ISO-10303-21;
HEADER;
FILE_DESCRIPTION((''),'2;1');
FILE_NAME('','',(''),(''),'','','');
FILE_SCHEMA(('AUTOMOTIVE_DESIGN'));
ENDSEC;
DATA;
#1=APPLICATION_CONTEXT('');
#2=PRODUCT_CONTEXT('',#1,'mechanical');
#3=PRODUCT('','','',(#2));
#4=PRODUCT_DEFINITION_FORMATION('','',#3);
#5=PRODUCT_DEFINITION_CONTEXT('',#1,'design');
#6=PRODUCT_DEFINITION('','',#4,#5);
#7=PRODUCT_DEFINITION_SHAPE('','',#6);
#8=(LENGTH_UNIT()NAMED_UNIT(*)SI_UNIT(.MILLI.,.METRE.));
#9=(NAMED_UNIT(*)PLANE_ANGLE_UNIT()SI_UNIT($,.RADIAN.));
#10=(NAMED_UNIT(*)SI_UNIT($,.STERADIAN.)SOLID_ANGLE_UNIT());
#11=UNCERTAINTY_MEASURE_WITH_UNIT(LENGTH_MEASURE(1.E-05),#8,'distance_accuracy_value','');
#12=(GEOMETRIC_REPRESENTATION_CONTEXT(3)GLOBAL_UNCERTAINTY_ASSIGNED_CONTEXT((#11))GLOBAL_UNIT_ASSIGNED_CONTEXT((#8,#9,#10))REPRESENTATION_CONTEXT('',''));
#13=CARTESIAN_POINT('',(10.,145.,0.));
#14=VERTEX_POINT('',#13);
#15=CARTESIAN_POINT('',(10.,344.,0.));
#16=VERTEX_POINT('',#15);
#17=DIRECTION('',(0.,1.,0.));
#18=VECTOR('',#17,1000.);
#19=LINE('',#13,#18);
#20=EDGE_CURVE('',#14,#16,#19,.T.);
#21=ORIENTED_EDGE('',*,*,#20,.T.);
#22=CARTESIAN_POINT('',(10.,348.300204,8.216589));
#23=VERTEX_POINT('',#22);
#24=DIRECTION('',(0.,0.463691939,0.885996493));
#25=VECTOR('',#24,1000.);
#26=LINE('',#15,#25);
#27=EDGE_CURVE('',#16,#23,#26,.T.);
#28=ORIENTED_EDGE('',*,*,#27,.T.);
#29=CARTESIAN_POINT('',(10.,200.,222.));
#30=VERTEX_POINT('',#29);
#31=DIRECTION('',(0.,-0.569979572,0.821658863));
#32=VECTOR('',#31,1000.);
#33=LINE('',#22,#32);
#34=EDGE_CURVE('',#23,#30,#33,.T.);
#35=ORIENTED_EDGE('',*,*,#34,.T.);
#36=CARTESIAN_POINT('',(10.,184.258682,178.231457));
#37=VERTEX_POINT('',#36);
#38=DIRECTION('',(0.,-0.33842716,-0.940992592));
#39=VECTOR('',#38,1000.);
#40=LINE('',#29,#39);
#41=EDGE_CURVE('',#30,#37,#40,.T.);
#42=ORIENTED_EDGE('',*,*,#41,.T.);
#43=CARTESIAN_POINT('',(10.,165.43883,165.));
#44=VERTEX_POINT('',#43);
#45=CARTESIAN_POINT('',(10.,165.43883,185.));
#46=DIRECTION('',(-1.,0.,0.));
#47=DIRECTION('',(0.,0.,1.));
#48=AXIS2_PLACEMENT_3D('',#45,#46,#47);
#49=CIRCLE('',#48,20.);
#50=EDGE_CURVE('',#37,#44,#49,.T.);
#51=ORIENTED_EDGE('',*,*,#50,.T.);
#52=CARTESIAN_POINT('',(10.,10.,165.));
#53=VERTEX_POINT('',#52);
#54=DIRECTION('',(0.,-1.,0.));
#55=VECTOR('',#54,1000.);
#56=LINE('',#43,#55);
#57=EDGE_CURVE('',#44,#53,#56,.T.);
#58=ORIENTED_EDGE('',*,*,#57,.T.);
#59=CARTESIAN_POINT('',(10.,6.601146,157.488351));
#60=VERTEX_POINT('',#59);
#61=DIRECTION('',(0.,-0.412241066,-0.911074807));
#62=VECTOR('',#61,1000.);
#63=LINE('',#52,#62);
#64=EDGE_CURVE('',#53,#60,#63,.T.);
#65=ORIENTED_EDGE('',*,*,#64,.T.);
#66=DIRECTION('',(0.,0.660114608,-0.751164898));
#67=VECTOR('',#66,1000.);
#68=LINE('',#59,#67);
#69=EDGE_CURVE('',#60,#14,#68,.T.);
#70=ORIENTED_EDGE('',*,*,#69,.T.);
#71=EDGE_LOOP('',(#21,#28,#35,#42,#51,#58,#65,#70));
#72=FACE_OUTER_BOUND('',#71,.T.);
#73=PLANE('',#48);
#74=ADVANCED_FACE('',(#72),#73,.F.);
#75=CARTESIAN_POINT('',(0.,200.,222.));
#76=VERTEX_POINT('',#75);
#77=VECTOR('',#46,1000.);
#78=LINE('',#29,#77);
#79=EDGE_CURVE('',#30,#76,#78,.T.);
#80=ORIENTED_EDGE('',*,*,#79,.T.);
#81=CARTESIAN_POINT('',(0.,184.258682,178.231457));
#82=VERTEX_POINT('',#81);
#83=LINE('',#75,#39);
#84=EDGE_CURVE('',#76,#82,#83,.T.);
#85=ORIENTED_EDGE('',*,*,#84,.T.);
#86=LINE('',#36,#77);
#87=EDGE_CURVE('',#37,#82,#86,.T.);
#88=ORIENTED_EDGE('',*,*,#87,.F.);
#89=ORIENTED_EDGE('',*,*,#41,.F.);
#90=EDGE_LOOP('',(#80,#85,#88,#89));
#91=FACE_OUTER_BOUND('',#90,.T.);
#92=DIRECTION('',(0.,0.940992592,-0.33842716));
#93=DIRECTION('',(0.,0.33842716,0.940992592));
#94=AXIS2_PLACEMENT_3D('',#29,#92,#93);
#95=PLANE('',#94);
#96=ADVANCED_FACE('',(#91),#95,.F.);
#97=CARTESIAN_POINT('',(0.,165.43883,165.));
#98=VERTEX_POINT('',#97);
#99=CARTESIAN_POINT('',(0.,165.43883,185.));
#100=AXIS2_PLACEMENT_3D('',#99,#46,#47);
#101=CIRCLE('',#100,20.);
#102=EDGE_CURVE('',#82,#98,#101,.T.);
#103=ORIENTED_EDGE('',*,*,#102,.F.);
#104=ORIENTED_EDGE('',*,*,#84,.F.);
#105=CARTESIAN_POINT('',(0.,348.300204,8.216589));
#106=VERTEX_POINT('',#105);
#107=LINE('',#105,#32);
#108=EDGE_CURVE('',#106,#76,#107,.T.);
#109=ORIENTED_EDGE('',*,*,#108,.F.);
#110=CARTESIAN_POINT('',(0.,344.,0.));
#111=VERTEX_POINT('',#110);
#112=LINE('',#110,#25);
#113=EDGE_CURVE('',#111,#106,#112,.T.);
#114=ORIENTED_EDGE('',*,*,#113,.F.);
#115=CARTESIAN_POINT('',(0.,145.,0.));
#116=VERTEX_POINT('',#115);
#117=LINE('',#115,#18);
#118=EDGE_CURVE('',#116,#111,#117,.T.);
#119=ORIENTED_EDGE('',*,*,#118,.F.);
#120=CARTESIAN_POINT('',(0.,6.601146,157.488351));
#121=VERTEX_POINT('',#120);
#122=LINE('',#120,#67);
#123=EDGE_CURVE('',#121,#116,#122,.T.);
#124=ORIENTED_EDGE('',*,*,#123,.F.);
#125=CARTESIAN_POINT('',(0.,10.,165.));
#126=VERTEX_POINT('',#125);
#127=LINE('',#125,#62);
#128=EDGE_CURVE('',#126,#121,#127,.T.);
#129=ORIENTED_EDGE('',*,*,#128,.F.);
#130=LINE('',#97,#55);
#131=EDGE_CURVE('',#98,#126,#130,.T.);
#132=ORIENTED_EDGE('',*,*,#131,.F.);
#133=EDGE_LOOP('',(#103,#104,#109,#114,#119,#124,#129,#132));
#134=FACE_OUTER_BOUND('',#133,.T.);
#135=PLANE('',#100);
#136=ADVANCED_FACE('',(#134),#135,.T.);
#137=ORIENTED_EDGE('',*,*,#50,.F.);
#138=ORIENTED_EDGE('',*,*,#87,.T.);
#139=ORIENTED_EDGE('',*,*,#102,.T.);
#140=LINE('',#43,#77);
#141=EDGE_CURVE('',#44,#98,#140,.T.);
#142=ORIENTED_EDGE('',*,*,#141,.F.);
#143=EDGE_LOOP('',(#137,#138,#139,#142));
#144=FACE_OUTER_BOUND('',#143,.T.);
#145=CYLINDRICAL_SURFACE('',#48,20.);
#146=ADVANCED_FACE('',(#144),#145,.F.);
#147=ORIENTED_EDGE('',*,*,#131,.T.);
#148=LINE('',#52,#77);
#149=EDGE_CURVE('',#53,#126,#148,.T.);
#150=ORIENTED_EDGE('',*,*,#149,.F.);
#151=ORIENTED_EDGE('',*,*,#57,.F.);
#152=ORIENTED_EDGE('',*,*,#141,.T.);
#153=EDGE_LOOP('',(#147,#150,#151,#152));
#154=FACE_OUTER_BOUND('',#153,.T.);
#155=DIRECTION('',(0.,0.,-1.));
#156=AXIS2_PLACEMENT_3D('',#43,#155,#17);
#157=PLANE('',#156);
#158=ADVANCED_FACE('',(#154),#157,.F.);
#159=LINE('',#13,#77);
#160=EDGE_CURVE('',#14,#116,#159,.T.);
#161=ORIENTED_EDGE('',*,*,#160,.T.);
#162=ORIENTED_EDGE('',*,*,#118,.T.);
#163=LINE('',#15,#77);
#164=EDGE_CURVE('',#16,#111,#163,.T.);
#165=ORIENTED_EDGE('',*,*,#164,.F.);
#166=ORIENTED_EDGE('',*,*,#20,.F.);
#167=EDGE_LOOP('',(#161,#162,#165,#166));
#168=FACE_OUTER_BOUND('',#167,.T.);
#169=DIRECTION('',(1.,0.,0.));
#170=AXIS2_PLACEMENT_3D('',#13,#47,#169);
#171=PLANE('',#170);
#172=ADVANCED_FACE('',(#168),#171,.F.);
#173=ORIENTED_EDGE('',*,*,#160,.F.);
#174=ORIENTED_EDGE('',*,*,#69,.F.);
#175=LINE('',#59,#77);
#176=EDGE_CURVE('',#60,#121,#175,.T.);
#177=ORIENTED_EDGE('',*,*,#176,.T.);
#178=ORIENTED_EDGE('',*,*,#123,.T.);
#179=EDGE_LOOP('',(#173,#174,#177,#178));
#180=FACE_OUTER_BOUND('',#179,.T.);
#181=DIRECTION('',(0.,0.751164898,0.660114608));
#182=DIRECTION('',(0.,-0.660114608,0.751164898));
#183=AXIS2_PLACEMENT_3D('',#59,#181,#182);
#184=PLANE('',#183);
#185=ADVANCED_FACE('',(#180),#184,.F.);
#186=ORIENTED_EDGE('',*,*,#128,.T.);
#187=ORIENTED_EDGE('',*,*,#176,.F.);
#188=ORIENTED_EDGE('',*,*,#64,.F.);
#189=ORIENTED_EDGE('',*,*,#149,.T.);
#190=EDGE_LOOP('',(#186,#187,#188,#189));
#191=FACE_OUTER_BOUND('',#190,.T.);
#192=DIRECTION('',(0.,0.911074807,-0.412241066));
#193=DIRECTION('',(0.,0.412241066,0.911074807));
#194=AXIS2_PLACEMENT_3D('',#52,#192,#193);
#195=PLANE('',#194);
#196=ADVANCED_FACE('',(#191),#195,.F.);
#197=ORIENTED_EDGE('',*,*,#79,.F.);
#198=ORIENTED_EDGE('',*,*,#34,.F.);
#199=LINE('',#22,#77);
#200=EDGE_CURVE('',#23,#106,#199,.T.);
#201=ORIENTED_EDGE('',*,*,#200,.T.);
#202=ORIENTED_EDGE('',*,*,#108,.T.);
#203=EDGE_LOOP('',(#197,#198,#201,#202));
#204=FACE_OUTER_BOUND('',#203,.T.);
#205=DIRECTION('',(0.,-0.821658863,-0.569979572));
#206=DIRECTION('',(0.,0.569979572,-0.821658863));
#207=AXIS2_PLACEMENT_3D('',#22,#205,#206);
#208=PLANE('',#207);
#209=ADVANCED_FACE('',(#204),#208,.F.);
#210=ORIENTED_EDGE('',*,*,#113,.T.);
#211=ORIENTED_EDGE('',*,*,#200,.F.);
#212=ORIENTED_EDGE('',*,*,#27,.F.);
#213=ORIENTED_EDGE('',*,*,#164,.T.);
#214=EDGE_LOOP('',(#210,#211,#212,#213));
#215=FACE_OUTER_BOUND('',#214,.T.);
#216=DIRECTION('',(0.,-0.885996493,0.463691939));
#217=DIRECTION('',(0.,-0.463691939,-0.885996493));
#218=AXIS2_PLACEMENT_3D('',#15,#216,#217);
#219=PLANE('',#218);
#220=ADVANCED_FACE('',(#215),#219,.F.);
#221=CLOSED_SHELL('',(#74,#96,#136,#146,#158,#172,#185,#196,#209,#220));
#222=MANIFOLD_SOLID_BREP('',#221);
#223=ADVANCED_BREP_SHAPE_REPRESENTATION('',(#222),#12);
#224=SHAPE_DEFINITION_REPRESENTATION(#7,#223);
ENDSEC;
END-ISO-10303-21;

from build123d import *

# Parameters (mm, degrees)
BOSS_EXTRUDE1_DEPTH = 10


with BuildPart() as part:
    # Sketch1 → Boss-Extrude1 (new body)
    with BuildSketch(Plane(origin=(0, 0, 0), x_dir=(0, 0, -1), z_dir=(1, 0, 0))):
        with BuildLine():
            Line((0, 145), (0, 344))
            Line((0, 344), (-8.216588633, 348.300204281))
            Line((-8.216588633, 348.300204281), (-222, 200))
            Line((-222, 200), (-178.231456798, 184.258681831))
            ThreePointArc((-178.231456798, 184.258681831), (-168.638904926, 176.941636961), (-165, 165.43883))
            Line((-165, 165.43883), (-165, 10))
            Line((-165, 10), (-157.488351016, 6.601146077))
            Line((-157.488351016, 6.601146077), (0, 145))
        make_face()
    extrude(amount=BOSS_EXTRUDE1_DEPTH)


solid = part.part
